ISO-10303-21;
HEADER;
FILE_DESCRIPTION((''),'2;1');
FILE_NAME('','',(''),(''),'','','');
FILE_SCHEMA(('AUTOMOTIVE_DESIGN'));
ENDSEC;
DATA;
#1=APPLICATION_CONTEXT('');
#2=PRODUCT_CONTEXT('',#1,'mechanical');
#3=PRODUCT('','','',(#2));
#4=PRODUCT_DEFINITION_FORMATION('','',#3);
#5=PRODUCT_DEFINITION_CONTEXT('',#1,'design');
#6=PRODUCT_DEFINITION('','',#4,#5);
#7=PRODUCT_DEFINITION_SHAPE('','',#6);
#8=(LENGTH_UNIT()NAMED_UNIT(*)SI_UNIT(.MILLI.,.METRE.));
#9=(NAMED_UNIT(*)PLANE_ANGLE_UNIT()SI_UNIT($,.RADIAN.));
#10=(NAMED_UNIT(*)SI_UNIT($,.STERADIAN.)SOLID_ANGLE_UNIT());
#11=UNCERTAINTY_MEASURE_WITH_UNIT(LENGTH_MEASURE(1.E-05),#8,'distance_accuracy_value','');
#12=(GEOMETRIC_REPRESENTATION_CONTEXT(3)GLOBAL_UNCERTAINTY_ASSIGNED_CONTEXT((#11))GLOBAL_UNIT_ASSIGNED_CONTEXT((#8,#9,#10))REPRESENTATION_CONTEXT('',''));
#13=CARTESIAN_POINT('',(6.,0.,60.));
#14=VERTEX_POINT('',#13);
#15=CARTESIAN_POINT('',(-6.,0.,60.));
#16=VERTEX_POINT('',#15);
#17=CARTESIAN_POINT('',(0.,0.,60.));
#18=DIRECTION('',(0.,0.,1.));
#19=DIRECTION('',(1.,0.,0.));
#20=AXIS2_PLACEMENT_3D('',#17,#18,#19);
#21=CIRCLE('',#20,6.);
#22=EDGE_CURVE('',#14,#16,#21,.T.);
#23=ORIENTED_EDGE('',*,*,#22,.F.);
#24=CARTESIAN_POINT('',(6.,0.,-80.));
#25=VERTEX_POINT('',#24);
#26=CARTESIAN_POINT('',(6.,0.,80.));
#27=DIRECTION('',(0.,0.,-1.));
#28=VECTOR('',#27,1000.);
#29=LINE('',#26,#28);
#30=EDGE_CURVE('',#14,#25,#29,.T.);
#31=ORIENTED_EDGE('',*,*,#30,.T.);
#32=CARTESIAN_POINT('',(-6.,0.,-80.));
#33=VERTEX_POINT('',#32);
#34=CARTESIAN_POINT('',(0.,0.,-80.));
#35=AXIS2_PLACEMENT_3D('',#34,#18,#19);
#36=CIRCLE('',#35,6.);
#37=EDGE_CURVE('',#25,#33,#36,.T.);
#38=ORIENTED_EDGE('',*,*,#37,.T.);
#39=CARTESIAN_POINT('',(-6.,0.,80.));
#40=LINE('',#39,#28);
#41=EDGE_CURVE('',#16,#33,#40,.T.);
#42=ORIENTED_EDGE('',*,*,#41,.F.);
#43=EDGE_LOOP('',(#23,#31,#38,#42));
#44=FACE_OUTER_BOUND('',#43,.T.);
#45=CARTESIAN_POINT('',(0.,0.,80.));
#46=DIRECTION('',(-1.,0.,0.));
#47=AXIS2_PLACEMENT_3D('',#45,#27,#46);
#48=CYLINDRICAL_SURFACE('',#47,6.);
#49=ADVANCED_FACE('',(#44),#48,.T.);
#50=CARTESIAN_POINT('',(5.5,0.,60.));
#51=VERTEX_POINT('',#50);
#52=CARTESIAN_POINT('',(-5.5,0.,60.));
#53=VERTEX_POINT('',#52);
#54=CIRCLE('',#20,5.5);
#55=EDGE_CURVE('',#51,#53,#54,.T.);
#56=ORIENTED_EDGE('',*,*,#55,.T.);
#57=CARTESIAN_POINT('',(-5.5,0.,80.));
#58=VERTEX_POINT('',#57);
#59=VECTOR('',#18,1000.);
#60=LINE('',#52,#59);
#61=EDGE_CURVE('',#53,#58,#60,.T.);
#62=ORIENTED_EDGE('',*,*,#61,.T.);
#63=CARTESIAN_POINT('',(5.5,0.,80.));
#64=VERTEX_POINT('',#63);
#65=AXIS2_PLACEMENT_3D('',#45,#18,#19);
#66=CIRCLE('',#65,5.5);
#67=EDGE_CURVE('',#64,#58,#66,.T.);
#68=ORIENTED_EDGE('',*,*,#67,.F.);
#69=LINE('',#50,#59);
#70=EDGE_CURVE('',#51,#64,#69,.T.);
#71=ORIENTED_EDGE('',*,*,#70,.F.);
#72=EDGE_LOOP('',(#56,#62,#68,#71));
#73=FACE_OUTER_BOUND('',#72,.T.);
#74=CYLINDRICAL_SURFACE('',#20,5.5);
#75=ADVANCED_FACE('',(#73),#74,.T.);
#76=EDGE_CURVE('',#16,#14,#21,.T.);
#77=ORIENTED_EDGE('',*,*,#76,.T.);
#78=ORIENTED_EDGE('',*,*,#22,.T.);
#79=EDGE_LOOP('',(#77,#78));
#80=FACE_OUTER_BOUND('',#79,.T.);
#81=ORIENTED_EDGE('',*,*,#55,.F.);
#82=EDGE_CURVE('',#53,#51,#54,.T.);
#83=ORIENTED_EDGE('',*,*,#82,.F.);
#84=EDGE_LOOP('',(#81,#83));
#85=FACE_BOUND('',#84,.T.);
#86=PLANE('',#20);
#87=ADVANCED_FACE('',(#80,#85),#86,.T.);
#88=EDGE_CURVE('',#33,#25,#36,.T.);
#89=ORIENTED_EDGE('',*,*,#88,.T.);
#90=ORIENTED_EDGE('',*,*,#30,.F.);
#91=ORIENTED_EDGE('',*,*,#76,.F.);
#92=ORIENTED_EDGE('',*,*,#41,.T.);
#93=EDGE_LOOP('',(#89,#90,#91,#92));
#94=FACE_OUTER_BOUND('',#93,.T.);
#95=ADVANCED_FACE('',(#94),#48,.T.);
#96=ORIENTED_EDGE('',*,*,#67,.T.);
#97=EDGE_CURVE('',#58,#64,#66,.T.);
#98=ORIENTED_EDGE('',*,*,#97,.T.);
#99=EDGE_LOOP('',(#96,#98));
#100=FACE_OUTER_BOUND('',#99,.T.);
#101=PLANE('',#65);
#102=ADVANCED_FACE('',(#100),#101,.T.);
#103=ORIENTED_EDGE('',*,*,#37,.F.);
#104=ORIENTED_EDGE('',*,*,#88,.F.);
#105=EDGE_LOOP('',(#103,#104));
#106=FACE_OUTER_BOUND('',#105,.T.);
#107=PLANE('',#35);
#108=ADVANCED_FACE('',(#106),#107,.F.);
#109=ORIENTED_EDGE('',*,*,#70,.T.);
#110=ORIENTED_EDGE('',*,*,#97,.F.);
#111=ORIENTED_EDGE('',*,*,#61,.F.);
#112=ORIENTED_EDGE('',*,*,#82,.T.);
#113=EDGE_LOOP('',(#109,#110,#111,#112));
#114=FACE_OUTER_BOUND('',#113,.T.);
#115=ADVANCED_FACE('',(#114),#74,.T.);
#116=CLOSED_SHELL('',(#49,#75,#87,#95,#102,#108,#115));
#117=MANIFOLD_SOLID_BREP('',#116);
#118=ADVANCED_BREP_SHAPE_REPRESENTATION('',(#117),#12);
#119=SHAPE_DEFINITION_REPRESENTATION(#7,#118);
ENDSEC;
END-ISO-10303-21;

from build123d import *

# Parameters (mm, degrees)
SKETCH_1_R          = 6
EXTRUDE_3_DEPTH     = 80
SKETCH_3_R          = 6
SKETCH_3_R_2        = 5.5
CUT_EXTRUDE_1_DEPTH = 20


with BuildPart() as part:
    # 草图1 → 凸台-拉伸3 (new, symmetric)
    with BuildSketch(Plane.XY):
        Circle(SKETCH_1_R)
    extrude(amount=EXTRUDE_3_DEPTH, both=True)

    # 草图3 → 切除-拉伸1 (cut)
    with BuildSketch(Plane.XY.offset(80)):
        Circle(SKETCH_3_R)
        Circle(SKETCH_3_R_2, mode=Mode.SUBTRACT)
    extrude(amount=-CUT_EXTRUDE_1_DEPTH, mode=Mode.SUBTRACT)


solid = part.part
